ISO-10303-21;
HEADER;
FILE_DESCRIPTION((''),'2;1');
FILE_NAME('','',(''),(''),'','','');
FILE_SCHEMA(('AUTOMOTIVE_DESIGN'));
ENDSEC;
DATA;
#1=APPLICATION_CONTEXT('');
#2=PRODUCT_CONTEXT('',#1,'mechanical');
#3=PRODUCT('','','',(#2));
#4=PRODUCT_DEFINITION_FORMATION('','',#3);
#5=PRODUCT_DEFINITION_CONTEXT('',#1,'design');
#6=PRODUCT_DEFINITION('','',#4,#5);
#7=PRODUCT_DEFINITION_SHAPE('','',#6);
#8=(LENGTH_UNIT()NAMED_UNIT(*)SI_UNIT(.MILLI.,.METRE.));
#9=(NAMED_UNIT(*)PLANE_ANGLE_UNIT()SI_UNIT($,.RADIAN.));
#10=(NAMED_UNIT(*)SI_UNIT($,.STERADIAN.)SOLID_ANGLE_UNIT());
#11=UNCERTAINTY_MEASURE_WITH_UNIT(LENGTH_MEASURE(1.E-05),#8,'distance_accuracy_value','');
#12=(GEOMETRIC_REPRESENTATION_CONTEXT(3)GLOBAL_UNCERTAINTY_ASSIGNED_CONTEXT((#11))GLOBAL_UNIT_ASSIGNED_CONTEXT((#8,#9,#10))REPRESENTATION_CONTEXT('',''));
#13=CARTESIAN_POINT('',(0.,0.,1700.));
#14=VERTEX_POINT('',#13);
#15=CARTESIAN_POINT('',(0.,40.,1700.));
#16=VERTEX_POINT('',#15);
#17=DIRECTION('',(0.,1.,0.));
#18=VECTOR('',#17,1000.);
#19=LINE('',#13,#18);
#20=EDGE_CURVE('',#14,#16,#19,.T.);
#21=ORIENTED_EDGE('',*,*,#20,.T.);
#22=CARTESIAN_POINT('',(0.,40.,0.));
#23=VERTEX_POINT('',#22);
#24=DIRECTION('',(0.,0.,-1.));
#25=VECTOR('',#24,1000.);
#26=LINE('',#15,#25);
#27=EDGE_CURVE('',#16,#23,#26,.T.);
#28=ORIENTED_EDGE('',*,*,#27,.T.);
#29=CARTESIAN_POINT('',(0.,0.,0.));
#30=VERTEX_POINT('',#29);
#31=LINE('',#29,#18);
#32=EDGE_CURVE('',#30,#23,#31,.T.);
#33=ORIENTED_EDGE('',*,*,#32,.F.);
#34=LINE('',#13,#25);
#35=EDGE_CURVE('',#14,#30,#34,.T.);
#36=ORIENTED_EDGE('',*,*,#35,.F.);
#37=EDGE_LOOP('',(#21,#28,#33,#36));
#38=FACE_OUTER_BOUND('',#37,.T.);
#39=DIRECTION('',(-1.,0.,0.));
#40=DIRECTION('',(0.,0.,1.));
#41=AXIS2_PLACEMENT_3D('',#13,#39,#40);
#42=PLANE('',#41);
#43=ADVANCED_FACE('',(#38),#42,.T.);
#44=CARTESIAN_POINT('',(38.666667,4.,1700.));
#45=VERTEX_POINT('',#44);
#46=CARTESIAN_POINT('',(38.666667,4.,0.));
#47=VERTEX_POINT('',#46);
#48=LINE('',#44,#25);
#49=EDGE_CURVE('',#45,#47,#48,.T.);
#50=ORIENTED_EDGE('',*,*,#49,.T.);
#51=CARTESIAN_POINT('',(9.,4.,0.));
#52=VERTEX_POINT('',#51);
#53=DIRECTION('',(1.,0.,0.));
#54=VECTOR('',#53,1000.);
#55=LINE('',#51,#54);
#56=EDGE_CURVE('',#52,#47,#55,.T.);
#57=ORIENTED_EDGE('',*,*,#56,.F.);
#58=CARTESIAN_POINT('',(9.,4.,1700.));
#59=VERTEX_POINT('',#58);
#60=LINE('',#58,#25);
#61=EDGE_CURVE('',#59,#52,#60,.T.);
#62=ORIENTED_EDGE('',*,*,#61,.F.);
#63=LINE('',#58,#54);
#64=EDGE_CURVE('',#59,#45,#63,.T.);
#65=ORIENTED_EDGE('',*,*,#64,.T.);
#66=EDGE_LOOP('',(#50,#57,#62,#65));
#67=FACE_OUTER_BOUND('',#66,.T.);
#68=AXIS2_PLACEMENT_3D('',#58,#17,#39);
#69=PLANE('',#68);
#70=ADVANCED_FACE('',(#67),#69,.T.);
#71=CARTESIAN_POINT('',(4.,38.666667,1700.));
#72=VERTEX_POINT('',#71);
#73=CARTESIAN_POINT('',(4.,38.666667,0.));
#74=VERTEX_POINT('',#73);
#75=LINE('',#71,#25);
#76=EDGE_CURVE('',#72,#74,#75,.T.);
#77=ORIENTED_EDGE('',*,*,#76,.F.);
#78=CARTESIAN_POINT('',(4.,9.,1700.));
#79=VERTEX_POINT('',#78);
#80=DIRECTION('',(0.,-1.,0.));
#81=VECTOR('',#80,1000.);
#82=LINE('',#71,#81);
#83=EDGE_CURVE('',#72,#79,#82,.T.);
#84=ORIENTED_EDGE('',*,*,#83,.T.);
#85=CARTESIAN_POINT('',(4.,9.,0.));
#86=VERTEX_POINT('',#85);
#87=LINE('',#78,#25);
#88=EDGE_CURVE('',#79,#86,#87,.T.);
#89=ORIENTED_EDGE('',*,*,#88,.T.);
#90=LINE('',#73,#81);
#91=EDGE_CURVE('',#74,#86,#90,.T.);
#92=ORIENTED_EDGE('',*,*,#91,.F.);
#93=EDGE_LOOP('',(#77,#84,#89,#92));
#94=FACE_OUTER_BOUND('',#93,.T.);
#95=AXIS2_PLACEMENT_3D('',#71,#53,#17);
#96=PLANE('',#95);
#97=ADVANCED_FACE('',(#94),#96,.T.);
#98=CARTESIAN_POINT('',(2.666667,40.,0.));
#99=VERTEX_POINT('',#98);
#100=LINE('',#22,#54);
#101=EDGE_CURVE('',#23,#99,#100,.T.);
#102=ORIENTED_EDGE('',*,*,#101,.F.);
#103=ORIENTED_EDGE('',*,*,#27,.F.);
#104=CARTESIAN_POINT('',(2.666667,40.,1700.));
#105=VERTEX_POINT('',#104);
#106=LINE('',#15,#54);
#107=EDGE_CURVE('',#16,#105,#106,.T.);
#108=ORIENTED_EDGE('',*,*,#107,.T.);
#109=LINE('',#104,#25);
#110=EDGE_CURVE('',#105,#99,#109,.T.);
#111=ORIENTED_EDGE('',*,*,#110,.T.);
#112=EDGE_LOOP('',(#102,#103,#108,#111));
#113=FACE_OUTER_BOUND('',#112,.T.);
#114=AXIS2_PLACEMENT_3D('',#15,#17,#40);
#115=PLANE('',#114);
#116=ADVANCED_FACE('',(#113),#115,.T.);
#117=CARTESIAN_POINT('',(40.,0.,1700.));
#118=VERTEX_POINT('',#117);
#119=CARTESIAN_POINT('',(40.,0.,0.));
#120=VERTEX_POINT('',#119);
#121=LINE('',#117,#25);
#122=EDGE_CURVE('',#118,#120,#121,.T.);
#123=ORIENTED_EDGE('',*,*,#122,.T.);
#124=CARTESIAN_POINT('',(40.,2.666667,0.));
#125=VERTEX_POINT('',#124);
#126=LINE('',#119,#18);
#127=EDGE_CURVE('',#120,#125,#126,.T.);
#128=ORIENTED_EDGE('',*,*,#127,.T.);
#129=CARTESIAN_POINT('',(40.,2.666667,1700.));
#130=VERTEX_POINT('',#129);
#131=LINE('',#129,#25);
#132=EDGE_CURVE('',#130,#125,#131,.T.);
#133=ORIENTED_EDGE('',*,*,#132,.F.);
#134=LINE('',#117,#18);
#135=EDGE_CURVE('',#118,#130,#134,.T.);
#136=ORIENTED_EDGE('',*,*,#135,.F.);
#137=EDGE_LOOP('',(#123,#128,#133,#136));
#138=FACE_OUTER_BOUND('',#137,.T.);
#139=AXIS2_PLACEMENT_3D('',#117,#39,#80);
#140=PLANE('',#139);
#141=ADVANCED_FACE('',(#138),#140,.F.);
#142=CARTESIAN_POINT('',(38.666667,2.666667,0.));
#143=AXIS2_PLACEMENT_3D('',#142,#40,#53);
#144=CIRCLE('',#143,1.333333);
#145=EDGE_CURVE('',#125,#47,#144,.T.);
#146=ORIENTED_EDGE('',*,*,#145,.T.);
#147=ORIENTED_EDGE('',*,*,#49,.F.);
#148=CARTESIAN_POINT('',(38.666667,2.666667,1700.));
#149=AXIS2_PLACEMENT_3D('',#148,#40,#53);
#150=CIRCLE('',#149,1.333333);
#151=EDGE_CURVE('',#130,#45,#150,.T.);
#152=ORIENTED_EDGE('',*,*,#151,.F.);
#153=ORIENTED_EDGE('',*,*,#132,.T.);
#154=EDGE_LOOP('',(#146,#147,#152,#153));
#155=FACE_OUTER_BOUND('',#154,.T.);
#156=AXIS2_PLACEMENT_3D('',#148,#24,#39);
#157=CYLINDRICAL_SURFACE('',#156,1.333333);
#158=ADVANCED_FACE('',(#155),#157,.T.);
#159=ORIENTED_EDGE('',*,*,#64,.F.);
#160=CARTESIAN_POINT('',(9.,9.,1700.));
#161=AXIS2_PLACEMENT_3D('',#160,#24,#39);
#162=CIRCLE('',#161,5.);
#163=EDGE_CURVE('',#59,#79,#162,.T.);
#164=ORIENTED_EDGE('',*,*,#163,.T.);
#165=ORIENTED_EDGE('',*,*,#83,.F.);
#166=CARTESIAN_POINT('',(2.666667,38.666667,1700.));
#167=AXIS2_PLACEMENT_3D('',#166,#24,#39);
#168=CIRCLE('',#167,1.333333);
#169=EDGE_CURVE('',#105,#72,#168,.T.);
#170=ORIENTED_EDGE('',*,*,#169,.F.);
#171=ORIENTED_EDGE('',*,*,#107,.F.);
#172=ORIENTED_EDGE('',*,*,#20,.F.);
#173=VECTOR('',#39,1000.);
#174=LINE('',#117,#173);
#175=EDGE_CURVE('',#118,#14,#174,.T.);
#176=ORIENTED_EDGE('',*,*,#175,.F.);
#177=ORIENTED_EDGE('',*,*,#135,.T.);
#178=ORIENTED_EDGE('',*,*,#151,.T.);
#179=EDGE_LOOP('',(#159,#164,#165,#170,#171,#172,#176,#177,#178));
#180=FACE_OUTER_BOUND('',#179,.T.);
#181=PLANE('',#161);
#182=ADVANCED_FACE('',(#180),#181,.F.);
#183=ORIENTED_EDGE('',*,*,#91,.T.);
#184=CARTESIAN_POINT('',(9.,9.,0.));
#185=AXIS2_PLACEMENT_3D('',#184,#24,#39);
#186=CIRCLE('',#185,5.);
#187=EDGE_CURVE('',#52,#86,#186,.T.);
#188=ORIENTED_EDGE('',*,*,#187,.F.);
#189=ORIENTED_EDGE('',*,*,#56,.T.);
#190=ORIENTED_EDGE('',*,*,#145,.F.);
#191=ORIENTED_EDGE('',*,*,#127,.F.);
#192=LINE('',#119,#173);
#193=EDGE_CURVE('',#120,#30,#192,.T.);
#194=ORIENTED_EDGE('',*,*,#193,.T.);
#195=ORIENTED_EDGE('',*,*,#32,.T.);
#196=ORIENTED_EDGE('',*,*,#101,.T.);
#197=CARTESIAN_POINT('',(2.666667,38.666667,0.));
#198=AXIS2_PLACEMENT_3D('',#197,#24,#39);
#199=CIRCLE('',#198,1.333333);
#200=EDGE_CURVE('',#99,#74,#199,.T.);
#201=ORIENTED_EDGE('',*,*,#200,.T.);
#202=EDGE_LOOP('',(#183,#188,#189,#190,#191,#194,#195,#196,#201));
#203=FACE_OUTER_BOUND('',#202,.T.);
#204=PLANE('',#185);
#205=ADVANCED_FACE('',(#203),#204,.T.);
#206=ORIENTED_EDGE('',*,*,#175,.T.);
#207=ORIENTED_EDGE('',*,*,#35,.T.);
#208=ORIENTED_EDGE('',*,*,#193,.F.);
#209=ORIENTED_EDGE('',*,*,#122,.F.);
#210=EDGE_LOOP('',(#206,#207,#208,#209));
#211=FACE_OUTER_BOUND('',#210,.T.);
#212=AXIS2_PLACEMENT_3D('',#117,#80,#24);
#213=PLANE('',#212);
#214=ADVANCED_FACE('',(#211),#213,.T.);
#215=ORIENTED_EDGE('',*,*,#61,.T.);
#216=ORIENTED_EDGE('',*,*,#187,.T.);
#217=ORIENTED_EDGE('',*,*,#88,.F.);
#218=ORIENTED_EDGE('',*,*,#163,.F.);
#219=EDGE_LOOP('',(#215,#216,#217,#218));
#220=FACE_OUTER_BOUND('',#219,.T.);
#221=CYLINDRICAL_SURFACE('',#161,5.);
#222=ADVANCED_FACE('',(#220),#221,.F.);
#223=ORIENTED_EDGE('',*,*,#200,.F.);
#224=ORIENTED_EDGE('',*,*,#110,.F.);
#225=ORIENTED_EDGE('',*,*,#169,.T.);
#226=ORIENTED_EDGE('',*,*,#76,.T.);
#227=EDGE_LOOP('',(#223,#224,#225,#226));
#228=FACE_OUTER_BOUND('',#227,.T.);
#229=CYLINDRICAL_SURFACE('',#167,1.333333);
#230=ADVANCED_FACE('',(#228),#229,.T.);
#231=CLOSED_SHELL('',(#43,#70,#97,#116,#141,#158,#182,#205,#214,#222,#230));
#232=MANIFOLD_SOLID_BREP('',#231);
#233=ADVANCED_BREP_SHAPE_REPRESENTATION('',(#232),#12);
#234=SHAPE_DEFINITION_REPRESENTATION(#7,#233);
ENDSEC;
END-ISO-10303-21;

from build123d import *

# Parameters (mm, degrees)
BOSS_EXTRUDE1_DEPTH = 1700


with BuildPart() as part:
    # Sketch1 → Boss-Extrude1 (new body)
    with BuildSketch(Plane.XY):
        with BuildLine():
            Line((0, 0), (0, 40))
            Line((0, 40), (2.666666667, 40))
            ThreePointArc((2.666666667, 40), (3.609475708, 39.609475708), (4, 38.666666667))
            Line((4, 38.666666667), (4, 9))
            ThreePointArc((4, 9), (5.464466094, 5.464466094), (9, 4))
            Line((9, 4), (38.666666667, 4))
            ThreePointArc((38.666666667, 4), (39.609475708, 3.609475708), (40, 2.666666667))
            Line((40, 2.666666667), (40, 0))
            Line((40, 0), (0, 0))
        make_face()
    extrude(amount=BOSS_EXTRUDE1_DEPTH)


solid = part.part
